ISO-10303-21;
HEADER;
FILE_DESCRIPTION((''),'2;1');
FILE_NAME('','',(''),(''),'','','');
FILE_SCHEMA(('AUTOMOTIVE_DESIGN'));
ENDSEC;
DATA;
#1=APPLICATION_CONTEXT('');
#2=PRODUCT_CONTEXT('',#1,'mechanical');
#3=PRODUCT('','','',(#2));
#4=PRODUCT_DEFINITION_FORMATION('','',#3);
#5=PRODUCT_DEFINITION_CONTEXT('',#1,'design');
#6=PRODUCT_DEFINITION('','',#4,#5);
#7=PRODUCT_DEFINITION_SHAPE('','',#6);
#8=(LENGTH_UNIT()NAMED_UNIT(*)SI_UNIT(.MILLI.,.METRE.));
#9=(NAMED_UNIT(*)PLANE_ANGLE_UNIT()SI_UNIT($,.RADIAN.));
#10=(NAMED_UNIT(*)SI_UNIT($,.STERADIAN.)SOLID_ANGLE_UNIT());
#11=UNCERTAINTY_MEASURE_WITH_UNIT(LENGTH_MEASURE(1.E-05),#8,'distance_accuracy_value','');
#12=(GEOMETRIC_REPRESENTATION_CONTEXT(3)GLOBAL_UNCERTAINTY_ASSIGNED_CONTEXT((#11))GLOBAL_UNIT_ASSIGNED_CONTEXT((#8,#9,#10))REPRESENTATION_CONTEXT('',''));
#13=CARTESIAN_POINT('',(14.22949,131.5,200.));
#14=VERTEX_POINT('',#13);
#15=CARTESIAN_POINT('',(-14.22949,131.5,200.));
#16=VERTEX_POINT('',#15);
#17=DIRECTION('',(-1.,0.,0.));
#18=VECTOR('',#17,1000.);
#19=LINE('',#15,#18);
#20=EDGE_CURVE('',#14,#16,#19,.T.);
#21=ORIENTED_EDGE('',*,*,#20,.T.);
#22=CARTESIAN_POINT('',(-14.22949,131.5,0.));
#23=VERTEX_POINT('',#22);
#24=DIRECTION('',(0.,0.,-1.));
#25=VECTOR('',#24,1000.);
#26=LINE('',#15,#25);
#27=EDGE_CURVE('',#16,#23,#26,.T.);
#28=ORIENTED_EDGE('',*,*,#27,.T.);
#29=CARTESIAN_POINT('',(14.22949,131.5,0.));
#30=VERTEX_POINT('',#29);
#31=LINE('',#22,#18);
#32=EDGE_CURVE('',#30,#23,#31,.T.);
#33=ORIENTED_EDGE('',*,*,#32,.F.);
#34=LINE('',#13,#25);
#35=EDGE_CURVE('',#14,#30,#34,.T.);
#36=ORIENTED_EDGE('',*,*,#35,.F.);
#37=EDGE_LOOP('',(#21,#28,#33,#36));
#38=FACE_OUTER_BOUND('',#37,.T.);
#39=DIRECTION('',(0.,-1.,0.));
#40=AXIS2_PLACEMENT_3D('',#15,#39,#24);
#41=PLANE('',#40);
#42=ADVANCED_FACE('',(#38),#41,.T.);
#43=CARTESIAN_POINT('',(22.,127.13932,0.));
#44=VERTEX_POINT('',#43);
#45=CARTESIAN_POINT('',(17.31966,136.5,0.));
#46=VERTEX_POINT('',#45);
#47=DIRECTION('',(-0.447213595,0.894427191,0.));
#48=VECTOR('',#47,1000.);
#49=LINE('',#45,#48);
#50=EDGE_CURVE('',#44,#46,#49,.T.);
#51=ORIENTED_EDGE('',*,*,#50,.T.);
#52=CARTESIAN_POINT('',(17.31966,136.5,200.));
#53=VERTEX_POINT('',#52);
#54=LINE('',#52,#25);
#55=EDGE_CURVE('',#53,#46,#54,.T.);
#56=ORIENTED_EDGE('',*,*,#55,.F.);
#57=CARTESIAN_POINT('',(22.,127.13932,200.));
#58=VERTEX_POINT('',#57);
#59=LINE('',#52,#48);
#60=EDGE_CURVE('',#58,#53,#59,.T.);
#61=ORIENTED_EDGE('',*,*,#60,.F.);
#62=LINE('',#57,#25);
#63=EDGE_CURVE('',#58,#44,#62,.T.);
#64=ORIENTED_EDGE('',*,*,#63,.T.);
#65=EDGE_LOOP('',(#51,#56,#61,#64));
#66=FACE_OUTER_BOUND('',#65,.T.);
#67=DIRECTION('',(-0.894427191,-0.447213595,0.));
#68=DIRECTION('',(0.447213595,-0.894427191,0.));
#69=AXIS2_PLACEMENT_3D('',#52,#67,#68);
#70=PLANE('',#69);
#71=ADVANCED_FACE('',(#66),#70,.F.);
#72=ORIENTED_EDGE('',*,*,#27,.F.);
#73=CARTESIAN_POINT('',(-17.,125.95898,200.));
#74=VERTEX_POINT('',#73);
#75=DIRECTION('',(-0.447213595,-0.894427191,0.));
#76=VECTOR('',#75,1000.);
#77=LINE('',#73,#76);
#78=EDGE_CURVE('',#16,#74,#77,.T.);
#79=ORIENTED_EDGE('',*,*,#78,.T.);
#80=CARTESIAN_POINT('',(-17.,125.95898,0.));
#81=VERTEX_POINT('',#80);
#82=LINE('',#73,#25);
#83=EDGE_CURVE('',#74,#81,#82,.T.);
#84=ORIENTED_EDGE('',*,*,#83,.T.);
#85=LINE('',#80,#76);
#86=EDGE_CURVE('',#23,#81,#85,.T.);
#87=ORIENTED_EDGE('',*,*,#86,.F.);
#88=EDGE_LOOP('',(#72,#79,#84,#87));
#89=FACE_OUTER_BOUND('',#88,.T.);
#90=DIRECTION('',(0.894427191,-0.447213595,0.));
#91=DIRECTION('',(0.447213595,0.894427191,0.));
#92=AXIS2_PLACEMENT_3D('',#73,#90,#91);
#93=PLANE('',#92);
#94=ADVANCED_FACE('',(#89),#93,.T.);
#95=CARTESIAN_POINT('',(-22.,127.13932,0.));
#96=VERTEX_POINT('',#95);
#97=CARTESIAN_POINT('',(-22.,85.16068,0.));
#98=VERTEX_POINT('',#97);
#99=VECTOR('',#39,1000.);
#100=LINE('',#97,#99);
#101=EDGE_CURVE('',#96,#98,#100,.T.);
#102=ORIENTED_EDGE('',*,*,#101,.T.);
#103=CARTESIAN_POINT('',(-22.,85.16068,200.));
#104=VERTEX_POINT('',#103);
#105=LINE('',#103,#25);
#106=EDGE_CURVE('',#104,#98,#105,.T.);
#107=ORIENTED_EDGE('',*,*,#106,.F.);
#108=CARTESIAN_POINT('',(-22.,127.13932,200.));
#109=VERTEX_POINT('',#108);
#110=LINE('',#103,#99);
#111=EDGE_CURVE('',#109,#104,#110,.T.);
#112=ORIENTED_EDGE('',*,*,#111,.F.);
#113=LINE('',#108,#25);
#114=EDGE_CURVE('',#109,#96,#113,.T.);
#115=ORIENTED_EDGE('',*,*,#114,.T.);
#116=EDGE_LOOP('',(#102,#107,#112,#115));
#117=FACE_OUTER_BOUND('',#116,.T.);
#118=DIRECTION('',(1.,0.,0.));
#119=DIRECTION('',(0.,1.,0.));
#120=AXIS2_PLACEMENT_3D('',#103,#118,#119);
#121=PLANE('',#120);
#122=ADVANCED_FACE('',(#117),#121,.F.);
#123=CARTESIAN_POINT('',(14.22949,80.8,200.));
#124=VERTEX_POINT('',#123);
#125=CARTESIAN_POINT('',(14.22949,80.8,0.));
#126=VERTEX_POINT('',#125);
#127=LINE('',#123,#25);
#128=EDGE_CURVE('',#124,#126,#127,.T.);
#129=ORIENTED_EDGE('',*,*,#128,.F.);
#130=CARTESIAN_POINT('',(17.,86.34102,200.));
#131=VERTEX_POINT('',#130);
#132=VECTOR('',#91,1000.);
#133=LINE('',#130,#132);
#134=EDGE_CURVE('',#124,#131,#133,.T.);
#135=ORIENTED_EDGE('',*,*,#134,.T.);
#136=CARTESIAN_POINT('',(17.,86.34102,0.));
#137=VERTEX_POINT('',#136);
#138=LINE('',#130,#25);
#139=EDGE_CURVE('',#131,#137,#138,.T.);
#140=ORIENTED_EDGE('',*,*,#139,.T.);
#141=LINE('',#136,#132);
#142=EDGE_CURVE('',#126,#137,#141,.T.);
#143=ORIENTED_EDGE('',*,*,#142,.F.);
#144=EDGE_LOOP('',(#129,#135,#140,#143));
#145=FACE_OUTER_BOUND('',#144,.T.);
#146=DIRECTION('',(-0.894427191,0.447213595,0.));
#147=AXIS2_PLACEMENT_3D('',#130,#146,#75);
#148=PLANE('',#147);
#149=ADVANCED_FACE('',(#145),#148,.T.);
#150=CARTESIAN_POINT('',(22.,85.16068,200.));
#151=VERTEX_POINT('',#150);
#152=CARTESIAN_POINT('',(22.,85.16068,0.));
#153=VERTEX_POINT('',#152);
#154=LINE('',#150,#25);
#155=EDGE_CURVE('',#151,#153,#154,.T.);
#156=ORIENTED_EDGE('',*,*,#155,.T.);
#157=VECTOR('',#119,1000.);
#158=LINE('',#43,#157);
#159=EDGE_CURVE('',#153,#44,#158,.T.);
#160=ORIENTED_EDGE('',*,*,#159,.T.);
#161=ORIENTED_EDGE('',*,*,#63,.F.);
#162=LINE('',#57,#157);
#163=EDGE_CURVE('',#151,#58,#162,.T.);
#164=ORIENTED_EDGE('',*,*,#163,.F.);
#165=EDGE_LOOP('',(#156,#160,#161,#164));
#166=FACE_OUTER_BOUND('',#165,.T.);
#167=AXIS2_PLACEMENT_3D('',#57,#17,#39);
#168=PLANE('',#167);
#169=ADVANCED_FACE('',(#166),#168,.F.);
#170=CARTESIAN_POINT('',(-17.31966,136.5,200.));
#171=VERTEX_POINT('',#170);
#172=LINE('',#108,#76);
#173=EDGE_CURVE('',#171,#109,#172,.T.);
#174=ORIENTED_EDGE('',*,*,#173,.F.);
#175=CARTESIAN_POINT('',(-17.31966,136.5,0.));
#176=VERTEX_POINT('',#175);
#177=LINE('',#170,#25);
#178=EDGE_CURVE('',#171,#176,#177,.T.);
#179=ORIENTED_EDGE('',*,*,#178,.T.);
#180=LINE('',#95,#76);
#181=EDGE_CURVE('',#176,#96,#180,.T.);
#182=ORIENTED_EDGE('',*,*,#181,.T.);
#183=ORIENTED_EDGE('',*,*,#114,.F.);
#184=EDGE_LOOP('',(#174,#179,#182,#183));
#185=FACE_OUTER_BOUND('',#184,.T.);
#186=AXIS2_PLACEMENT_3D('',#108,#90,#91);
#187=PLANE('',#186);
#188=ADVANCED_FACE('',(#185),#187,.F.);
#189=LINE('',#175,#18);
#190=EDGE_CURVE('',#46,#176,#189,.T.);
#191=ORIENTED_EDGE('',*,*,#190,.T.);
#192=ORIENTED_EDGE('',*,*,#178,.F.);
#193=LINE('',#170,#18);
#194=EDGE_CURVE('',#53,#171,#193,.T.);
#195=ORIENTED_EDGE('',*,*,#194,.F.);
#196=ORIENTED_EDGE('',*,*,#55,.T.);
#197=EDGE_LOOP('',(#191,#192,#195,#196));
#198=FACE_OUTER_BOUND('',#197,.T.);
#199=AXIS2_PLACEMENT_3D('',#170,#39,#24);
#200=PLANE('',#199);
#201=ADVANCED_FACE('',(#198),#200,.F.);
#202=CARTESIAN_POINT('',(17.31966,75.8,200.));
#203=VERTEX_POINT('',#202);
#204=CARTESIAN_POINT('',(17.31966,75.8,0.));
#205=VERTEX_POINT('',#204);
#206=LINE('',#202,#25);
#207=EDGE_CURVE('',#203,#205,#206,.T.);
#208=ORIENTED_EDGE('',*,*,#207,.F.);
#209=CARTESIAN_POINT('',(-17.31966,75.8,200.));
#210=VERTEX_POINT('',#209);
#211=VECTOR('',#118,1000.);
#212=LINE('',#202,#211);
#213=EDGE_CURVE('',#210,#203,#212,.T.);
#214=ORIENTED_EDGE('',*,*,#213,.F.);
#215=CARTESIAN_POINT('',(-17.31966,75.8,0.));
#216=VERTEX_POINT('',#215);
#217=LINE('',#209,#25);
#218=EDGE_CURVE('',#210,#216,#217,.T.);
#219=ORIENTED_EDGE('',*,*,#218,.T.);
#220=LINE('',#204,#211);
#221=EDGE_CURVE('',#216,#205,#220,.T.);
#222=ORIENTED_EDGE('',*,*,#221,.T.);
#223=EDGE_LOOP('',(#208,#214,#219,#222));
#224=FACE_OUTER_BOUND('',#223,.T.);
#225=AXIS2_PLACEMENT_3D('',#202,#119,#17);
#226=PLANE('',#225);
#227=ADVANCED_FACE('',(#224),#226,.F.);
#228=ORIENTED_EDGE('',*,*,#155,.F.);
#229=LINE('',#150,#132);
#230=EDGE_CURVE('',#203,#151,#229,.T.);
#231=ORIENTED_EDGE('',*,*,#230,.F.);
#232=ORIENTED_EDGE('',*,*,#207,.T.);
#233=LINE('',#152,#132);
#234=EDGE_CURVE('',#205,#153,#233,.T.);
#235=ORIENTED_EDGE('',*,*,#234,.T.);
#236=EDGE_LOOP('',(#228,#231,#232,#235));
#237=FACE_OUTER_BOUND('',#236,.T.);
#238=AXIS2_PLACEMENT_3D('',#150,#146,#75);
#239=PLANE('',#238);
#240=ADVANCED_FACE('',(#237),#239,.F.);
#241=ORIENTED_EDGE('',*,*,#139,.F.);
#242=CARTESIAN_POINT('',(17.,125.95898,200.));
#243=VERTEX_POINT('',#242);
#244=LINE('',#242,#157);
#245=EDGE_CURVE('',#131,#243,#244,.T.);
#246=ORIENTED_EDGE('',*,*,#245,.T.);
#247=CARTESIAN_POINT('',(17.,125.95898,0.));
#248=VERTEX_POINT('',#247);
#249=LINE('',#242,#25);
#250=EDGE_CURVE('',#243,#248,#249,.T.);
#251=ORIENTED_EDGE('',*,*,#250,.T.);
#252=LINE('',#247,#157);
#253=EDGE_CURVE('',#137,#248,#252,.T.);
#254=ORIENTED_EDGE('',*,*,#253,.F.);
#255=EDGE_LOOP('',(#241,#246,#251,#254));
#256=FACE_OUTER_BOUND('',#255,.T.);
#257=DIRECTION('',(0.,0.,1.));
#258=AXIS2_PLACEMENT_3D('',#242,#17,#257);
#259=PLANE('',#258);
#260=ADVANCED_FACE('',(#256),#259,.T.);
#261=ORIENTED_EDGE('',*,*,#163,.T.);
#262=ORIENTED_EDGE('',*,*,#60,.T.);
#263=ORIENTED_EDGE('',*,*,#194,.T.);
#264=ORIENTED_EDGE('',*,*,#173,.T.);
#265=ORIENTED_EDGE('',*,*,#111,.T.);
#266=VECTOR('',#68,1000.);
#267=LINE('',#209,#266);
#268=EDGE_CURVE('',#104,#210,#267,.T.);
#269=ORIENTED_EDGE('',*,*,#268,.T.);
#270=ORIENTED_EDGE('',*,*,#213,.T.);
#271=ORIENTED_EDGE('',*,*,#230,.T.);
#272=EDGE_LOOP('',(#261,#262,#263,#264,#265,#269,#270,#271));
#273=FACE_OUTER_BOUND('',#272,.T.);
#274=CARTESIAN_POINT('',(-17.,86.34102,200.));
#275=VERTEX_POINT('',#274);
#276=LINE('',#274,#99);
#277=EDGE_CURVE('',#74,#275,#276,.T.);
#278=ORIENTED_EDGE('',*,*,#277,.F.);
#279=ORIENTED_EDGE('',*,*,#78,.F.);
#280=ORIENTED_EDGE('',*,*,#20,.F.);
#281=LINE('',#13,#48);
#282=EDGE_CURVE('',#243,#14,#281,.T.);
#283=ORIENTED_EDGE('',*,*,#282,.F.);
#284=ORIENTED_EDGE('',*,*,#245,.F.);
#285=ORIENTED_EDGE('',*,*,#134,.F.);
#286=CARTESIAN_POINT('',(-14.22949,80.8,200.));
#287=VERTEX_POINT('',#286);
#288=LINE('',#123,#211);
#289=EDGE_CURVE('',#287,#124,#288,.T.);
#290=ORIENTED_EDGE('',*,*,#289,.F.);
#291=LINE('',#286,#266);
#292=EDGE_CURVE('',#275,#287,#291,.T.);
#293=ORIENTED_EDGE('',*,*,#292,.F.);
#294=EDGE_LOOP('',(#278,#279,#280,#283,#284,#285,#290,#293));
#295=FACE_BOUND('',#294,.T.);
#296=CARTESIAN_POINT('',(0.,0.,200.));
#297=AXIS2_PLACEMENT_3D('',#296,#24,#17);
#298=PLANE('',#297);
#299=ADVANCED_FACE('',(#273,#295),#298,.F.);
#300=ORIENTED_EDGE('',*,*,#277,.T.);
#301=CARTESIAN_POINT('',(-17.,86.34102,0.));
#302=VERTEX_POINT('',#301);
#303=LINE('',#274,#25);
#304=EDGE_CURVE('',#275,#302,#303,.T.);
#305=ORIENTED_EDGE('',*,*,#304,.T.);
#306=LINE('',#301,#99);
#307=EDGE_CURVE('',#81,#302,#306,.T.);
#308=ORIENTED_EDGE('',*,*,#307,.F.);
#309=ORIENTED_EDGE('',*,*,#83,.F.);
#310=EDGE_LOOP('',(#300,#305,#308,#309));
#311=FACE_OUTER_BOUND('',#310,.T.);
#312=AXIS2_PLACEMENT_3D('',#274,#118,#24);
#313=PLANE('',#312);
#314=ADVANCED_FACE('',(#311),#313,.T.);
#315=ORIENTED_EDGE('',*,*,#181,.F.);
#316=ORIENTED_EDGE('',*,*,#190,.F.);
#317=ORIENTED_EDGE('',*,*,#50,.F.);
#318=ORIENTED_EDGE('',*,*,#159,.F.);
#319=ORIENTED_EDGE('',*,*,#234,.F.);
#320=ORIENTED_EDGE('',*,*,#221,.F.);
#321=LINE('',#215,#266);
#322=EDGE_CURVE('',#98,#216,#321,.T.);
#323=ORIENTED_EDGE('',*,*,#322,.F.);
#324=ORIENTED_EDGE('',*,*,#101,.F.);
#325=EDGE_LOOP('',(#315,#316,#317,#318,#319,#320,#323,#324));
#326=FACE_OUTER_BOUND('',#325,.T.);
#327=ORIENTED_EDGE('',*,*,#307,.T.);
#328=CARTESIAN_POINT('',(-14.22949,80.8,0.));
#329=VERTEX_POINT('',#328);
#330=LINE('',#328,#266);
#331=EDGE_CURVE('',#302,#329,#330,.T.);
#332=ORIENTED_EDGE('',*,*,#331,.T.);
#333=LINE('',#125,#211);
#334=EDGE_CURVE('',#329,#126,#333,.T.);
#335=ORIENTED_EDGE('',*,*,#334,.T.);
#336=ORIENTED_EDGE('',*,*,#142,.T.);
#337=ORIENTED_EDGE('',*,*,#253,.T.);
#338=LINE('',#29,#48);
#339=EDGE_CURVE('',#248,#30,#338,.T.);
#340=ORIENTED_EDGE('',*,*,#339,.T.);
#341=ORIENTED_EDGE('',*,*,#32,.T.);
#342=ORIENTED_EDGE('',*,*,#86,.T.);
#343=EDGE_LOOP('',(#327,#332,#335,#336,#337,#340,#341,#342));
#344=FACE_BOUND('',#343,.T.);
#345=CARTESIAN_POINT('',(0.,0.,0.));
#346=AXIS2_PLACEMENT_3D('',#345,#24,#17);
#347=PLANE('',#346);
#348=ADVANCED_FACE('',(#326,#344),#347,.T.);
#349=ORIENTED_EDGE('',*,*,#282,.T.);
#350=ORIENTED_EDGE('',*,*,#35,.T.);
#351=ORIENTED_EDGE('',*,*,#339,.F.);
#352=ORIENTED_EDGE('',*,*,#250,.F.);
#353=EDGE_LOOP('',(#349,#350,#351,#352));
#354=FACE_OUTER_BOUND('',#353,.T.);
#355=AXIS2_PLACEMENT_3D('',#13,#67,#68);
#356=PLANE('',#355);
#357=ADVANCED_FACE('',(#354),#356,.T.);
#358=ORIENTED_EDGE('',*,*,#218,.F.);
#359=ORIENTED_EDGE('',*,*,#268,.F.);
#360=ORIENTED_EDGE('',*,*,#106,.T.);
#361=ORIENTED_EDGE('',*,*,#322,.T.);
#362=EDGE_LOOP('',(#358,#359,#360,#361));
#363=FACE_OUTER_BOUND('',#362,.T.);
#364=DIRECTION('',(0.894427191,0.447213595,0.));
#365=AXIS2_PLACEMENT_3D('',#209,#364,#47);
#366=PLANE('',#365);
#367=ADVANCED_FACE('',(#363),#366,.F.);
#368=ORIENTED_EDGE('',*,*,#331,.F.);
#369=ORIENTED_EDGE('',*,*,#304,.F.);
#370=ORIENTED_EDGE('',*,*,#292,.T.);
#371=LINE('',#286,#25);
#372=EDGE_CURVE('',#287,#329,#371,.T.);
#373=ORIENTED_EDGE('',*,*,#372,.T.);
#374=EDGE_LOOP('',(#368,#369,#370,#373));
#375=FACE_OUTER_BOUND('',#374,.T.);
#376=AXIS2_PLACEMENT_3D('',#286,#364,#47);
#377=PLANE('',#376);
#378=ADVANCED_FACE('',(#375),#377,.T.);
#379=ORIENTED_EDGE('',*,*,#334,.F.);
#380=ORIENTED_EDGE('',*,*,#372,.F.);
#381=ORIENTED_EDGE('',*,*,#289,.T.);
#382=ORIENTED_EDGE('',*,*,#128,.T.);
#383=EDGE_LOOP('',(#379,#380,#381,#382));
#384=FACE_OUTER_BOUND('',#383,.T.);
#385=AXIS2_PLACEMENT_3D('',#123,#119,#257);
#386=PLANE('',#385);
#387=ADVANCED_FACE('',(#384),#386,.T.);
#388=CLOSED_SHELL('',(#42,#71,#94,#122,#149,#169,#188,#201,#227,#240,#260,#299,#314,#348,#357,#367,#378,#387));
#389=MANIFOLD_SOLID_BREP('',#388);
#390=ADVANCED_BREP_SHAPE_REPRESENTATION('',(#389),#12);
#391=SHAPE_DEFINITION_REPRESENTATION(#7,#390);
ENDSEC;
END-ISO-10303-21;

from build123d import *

# Parameters (mm, degrees)
BOSS_EXTRUDE1_DEPTH = 200


with BuildPart() as part:
    # Sketch1 → Boss-Extrude1 (new body)
    with BuildSketch(Plane.XY):
        Polygon((-17.319660113, 136.5), (17.319660113, 136.5), (22, 127.139320225), (22, 85.160679775), (17.319660113, 75.8), (-17.319660113, 75.8), (-22, 85.160679775), (-22, 127.139320225), align=None)
        Polygon((-14.229490169, 131.5), (14.229490169, 131.5), (17, 125.958980338), (17, 86.341019662), (14.229490169, 80.8), (-14.229490169, 80.8), (-17, 86.341019662), (-17, 125.958980338), align=None, mode=Mode.SUBTRACT)
    extrude(amount=BOSS_EXTRUDE1_DEPTH)


solid = part.part
